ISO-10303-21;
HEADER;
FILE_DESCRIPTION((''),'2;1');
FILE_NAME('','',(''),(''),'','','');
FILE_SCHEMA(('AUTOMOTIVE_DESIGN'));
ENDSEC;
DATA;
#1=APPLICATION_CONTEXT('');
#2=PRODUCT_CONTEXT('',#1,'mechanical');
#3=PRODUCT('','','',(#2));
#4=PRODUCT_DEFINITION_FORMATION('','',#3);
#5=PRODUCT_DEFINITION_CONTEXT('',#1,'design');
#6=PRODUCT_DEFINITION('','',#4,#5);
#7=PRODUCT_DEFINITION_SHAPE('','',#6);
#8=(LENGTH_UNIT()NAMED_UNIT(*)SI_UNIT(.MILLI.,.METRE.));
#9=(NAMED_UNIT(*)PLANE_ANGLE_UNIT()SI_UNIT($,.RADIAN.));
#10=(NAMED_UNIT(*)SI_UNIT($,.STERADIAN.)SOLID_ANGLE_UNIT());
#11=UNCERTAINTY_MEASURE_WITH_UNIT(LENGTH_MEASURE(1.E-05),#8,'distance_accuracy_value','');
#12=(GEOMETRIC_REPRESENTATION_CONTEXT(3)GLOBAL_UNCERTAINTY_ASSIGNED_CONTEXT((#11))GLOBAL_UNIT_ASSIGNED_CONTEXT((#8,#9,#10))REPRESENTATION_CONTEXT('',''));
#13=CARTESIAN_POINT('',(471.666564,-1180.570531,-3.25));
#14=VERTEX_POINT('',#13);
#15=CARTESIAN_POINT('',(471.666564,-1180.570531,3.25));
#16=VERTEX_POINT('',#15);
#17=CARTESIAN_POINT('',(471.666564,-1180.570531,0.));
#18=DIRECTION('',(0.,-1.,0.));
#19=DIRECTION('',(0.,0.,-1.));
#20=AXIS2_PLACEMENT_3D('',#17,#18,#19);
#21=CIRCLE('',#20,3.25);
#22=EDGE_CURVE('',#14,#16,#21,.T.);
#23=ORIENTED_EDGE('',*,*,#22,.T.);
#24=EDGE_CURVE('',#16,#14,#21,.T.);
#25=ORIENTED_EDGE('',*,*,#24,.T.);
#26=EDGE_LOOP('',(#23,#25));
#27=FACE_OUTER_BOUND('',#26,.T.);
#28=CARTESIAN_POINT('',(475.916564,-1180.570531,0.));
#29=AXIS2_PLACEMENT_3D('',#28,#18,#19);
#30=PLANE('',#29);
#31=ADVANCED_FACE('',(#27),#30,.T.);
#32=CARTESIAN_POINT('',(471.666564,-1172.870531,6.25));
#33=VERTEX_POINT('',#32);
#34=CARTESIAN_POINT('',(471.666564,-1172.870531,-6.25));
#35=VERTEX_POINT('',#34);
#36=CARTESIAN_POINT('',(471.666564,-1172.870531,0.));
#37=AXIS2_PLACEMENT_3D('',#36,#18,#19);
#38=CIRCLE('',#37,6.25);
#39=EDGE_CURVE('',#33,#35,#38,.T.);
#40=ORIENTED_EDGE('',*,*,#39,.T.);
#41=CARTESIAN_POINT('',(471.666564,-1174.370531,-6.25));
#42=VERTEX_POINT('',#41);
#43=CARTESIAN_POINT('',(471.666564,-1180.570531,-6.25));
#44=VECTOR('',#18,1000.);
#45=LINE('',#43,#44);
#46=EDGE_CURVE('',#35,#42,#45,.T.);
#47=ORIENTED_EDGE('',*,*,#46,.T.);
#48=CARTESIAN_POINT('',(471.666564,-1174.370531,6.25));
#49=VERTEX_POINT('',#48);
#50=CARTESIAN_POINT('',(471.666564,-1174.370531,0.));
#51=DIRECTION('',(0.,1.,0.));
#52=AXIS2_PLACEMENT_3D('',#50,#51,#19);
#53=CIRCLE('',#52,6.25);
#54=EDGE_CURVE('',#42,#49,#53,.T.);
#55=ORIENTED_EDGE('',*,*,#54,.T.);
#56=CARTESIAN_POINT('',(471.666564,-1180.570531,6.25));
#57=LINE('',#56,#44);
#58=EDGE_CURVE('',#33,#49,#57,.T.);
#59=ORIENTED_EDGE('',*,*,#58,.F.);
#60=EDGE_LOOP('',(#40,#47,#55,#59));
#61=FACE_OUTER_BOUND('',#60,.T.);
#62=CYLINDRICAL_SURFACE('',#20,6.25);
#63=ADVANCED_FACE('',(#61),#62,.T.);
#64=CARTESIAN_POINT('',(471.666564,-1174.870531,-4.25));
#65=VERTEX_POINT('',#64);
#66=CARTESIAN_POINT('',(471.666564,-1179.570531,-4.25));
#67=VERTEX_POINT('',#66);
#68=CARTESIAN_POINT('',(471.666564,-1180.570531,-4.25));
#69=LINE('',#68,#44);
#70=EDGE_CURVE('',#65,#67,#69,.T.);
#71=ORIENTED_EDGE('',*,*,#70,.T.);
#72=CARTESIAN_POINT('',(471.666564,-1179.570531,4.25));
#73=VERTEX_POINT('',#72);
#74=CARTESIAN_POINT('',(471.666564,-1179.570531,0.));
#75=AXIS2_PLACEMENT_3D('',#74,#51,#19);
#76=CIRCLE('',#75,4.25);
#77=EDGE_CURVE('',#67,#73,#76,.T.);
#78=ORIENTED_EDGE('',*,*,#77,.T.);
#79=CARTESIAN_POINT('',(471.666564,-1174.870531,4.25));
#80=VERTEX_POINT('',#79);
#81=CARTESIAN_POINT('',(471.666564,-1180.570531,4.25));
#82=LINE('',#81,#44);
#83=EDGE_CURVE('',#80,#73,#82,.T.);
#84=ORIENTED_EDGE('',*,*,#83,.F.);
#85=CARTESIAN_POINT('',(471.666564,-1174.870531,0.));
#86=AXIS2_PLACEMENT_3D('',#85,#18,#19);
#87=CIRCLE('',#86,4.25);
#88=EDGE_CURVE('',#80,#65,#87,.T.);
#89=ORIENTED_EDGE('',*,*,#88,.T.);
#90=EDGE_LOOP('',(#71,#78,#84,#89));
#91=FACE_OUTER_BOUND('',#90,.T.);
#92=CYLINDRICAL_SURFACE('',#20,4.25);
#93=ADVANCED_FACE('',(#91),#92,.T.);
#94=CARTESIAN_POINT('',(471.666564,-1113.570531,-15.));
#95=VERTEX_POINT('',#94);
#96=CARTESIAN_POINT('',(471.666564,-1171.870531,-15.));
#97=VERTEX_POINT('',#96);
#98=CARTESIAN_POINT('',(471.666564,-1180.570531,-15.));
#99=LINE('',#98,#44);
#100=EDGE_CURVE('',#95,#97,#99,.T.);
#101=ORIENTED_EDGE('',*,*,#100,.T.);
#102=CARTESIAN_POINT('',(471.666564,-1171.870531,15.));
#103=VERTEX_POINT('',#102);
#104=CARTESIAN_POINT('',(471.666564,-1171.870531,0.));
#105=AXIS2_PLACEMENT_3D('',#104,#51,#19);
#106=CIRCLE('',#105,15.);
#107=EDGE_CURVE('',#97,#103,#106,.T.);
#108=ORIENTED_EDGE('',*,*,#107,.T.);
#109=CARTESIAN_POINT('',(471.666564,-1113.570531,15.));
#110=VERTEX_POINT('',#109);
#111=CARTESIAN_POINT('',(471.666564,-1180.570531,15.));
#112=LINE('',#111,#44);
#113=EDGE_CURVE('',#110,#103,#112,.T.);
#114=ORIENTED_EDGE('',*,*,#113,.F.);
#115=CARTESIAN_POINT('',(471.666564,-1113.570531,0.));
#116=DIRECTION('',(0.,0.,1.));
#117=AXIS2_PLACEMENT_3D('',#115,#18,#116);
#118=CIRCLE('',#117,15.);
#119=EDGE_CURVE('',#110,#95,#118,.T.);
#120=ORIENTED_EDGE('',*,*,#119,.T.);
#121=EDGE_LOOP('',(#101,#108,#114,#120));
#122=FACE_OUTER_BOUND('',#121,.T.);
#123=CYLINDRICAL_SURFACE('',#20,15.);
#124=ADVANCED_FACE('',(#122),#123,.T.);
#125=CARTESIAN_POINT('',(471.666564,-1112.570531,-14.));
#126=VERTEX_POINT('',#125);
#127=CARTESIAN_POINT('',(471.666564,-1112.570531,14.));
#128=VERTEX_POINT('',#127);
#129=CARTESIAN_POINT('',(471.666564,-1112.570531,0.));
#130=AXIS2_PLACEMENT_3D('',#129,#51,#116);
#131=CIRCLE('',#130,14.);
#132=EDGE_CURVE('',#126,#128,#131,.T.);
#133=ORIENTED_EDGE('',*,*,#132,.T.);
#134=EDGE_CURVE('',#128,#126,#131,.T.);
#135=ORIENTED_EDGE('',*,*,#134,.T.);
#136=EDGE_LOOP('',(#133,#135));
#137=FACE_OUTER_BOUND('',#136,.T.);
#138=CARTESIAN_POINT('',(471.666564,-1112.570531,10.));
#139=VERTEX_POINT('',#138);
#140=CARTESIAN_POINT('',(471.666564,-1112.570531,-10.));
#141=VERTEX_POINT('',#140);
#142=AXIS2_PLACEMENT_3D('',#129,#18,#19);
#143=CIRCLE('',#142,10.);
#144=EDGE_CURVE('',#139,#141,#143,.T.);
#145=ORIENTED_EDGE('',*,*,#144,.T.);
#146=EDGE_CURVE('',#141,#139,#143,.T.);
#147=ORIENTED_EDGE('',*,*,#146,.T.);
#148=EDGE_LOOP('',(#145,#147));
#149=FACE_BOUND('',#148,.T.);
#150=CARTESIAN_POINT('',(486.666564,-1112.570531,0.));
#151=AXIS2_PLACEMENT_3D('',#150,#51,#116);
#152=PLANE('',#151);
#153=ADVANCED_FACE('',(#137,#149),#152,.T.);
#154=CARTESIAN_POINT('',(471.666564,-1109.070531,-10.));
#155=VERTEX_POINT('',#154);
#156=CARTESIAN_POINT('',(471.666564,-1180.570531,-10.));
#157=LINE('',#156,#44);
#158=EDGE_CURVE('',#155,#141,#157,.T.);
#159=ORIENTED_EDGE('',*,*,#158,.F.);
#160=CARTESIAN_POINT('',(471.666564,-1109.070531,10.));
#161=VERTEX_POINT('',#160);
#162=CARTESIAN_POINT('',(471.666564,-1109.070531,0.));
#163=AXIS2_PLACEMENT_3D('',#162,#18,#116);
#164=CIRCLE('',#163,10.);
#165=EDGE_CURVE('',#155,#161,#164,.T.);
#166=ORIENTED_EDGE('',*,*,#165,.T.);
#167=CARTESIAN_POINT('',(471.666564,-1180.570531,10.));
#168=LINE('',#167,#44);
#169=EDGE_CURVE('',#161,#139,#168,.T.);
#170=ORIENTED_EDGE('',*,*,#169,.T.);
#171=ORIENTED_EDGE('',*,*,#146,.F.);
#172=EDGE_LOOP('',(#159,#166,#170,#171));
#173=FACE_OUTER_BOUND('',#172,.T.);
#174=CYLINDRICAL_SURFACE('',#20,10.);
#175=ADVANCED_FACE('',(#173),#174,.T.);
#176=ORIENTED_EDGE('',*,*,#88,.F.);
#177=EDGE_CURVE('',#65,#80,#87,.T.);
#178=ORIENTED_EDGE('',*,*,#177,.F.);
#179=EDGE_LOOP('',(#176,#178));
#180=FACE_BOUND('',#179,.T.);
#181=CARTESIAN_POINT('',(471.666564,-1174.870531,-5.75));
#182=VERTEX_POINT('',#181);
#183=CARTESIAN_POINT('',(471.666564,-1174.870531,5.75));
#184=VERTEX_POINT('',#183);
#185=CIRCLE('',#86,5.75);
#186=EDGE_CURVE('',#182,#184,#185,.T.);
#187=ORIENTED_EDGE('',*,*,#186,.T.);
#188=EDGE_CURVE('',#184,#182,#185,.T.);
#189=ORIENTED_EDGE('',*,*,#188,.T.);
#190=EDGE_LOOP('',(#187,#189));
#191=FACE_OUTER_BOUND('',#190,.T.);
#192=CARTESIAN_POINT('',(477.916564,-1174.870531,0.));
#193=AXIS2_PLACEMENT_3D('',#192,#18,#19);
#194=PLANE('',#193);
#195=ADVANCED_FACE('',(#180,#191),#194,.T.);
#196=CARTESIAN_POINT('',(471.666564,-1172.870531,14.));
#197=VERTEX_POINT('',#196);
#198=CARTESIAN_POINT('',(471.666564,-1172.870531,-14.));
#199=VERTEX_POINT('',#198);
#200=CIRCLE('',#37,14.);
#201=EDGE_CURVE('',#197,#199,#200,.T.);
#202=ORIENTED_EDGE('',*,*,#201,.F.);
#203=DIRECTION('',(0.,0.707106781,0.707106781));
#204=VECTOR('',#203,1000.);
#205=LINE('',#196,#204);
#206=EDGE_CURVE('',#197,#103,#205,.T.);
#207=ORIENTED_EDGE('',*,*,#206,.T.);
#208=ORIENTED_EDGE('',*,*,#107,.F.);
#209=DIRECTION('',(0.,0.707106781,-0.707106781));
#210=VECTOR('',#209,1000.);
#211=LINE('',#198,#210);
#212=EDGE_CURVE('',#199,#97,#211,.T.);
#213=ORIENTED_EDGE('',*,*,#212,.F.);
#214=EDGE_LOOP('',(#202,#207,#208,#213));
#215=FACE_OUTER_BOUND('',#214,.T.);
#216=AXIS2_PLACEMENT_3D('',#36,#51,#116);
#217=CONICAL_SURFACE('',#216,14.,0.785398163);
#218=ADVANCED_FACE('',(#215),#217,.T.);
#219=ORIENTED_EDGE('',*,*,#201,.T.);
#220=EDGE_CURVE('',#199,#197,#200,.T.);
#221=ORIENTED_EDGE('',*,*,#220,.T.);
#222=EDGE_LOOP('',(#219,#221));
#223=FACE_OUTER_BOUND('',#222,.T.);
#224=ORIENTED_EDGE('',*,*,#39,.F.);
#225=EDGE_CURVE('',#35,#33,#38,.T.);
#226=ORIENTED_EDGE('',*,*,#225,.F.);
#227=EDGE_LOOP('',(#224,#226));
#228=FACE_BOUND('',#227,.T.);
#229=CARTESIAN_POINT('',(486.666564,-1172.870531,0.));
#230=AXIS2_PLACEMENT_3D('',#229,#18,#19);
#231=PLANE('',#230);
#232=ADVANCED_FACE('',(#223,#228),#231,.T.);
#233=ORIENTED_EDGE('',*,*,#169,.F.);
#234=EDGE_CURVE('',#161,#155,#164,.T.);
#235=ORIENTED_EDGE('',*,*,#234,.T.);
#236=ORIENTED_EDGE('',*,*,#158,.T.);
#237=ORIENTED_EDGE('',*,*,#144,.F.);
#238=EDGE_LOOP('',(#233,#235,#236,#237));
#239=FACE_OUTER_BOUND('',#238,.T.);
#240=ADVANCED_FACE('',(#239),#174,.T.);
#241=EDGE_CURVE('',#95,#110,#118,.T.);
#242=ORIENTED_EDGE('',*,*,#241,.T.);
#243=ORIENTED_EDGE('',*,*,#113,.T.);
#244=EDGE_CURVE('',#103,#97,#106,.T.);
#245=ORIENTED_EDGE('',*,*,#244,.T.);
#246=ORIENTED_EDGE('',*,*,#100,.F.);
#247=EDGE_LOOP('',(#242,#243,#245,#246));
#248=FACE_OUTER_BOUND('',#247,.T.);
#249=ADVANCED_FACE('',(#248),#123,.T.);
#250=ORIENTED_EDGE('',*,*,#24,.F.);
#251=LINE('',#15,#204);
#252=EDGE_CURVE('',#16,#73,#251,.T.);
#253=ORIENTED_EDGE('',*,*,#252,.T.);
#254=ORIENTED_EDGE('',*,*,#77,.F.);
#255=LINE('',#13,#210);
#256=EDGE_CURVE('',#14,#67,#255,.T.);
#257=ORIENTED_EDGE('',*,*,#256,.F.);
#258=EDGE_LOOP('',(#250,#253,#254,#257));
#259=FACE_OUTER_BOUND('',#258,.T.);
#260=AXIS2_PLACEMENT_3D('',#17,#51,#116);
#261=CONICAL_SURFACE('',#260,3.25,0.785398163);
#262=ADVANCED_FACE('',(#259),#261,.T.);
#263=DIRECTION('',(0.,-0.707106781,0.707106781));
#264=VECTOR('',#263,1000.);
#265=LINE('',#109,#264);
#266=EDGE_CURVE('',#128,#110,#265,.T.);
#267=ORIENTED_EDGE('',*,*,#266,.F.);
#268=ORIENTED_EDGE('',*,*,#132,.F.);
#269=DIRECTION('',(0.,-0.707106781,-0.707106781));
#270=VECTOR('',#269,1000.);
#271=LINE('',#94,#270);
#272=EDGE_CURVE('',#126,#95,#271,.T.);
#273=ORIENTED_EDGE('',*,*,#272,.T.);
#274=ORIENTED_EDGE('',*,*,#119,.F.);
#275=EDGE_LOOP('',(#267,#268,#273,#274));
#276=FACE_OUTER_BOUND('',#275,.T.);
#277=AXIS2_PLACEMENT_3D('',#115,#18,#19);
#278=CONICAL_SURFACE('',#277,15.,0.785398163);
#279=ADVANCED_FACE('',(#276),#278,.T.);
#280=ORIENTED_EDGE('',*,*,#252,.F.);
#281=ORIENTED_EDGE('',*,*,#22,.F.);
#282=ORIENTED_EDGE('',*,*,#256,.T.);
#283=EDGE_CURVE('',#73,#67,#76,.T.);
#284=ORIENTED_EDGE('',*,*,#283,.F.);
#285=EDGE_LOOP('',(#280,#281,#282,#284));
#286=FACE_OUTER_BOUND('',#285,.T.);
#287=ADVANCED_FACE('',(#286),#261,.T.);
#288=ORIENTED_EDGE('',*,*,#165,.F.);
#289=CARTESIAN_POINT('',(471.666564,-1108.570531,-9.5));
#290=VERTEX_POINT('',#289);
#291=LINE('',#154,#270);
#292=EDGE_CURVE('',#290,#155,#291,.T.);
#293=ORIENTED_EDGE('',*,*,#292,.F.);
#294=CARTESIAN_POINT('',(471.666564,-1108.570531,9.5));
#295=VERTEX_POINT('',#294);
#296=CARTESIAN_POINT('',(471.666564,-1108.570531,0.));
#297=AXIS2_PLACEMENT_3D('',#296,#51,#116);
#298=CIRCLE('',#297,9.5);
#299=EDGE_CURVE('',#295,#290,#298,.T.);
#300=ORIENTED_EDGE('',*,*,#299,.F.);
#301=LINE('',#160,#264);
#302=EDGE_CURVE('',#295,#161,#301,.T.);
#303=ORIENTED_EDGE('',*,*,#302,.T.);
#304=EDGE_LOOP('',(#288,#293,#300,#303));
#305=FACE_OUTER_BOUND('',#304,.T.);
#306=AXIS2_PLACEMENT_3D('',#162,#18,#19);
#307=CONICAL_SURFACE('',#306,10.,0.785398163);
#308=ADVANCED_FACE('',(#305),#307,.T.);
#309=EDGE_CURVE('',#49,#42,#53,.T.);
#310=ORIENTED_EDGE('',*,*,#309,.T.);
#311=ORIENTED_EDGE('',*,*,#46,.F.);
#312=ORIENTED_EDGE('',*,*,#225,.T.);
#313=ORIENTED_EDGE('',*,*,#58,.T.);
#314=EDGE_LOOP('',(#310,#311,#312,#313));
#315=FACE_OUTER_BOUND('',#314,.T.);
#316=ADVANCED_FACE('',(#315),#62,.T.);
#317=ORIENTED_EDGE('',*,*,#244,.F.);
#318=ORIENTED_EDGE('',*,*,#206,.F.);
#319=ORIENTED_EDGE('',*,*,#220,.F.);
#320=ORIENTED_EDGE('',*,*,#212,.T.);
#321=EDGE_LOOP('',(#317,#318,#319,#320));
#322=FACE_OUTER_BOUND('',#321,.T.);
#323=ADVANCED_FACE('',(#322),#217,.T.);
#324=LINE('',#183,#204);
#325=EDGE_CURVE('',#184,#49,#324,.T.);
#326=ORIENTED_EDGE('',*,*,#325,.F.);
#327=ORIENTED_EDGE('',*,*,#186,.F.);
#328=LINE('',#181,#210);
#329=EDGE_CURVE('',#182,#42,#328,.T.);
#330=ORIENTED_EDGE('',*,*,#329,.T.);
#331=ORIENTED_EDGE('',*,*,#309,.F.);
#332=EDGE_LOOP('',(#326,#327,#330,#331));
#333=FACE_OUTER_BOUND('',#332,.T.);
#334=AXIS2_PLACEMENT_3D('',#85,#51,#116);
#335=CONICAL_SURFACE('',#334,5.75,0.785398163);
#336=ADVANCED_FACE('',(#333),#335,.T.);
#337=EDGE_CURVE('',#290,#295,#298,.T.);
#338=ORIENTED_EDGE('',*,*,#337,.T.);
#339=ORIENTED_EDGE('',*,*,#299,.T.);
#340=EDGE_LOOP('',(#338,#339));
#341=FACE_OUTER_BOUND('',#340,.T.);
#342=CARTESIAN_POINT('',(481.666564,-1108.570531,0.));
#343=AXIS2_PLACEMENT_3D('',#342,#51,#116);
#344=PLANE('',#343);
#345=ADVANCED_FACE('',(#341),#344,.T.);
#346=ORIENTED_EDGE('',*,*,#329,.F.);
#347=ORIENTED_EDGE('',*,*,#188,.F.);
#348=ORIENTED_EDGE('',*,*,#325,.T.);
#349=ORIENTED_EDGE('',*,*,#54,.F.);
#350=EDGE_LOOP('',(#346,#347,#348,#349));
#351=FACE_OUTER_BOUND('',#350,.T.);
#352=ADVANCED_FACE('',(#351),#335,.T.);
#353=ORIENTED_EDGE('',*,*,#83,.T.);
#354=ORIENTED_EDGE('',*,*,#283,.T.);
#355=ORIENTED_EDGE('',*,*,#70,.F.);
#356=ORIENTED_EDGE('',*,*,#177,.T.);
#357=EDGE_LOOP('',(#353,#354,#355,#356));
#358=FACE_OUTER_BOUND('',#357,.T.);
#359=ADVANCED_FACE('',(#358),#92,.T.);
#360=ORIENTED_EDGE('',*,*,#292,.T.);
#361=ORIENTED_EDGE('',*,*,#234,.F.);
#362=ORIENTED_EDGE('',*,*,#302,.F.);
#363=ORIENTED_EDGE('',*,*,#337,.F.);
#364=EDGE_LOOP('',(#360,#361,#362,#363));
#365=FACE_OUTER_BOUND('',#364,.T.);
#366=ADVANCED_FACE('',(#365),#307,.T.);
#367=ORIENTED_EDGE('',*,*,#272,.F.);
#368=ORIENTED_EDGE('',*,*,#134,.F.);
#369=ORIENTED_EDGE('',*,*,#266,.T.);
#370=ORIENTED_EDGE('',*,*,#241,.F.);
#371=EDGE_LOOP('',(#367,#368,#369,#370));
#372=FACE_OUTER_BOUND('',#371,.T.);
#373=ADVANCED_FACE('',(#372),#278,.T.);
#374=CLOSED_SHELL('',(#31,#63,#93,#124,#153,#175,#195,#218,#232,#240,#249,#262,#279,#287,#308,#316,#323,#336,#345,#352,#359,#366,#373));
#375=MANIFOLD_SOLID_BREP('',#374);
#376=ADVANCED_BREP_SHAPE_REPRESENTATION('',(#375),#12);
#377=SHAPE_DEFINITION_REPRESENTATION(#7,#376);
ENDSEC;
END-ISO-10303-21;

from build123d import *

# Parameters (mm, degrees)
CHAMFER1_SIZE = 1
CHAMFER2_SIZE = 0.5


with BuildPart() as part:
    # Sketch1 → Revolve1 (revolve)
    with BuildSketch(Plane.XY, mode=Mode.PRIVATE) as revolve1_sk:
        Polygon((486.666563646, -1172.870531067), (486.666563646, -1112.570531067), (481.666563646, -1112.570531067), (481.666563646, -1108.570531067), (471.666563646, -1108.570531067), (471.666563646, -1180.570531067), (475.916563646, -1180.570531067), (475.916563646, -1174.870531067), (477.916563646, -1174.870531067), (477.916563646, -1172.870531067), align=None)
    revolve(revolve1_sk.sketch.rotate(Axis((471.666563646, -1180.570531067, 0), (0, 1, 0)), 90), axis=Axis((471.666563646, -1180.570531067, 0), (0, 1, 0)))

    # Chamfer1
    chamfer1_edges = [part.edges().sort_by_distance(p)[0] for p in [
        (471.666563646, -1112.570531067, 15),
        (471.666563646, -1172.870531067, 15),
        (471.666563646, -1180.570531067, 4.25),
    ]]
    chamfer(chamfer1_edges, length=CHAMFER1_SIZE)

    # Chamfer2
    chamfer2_edges = [part.edges().sort_by_distance(p)[0] for p in [
        (471.666563646, -1108.570531067, 10),
        (471.666563646, -1174.870531067, 6.25),
    ]]
    chamfer(chamfer2_edges, length=CHAMFER2_SIZE)


solid = part.part
